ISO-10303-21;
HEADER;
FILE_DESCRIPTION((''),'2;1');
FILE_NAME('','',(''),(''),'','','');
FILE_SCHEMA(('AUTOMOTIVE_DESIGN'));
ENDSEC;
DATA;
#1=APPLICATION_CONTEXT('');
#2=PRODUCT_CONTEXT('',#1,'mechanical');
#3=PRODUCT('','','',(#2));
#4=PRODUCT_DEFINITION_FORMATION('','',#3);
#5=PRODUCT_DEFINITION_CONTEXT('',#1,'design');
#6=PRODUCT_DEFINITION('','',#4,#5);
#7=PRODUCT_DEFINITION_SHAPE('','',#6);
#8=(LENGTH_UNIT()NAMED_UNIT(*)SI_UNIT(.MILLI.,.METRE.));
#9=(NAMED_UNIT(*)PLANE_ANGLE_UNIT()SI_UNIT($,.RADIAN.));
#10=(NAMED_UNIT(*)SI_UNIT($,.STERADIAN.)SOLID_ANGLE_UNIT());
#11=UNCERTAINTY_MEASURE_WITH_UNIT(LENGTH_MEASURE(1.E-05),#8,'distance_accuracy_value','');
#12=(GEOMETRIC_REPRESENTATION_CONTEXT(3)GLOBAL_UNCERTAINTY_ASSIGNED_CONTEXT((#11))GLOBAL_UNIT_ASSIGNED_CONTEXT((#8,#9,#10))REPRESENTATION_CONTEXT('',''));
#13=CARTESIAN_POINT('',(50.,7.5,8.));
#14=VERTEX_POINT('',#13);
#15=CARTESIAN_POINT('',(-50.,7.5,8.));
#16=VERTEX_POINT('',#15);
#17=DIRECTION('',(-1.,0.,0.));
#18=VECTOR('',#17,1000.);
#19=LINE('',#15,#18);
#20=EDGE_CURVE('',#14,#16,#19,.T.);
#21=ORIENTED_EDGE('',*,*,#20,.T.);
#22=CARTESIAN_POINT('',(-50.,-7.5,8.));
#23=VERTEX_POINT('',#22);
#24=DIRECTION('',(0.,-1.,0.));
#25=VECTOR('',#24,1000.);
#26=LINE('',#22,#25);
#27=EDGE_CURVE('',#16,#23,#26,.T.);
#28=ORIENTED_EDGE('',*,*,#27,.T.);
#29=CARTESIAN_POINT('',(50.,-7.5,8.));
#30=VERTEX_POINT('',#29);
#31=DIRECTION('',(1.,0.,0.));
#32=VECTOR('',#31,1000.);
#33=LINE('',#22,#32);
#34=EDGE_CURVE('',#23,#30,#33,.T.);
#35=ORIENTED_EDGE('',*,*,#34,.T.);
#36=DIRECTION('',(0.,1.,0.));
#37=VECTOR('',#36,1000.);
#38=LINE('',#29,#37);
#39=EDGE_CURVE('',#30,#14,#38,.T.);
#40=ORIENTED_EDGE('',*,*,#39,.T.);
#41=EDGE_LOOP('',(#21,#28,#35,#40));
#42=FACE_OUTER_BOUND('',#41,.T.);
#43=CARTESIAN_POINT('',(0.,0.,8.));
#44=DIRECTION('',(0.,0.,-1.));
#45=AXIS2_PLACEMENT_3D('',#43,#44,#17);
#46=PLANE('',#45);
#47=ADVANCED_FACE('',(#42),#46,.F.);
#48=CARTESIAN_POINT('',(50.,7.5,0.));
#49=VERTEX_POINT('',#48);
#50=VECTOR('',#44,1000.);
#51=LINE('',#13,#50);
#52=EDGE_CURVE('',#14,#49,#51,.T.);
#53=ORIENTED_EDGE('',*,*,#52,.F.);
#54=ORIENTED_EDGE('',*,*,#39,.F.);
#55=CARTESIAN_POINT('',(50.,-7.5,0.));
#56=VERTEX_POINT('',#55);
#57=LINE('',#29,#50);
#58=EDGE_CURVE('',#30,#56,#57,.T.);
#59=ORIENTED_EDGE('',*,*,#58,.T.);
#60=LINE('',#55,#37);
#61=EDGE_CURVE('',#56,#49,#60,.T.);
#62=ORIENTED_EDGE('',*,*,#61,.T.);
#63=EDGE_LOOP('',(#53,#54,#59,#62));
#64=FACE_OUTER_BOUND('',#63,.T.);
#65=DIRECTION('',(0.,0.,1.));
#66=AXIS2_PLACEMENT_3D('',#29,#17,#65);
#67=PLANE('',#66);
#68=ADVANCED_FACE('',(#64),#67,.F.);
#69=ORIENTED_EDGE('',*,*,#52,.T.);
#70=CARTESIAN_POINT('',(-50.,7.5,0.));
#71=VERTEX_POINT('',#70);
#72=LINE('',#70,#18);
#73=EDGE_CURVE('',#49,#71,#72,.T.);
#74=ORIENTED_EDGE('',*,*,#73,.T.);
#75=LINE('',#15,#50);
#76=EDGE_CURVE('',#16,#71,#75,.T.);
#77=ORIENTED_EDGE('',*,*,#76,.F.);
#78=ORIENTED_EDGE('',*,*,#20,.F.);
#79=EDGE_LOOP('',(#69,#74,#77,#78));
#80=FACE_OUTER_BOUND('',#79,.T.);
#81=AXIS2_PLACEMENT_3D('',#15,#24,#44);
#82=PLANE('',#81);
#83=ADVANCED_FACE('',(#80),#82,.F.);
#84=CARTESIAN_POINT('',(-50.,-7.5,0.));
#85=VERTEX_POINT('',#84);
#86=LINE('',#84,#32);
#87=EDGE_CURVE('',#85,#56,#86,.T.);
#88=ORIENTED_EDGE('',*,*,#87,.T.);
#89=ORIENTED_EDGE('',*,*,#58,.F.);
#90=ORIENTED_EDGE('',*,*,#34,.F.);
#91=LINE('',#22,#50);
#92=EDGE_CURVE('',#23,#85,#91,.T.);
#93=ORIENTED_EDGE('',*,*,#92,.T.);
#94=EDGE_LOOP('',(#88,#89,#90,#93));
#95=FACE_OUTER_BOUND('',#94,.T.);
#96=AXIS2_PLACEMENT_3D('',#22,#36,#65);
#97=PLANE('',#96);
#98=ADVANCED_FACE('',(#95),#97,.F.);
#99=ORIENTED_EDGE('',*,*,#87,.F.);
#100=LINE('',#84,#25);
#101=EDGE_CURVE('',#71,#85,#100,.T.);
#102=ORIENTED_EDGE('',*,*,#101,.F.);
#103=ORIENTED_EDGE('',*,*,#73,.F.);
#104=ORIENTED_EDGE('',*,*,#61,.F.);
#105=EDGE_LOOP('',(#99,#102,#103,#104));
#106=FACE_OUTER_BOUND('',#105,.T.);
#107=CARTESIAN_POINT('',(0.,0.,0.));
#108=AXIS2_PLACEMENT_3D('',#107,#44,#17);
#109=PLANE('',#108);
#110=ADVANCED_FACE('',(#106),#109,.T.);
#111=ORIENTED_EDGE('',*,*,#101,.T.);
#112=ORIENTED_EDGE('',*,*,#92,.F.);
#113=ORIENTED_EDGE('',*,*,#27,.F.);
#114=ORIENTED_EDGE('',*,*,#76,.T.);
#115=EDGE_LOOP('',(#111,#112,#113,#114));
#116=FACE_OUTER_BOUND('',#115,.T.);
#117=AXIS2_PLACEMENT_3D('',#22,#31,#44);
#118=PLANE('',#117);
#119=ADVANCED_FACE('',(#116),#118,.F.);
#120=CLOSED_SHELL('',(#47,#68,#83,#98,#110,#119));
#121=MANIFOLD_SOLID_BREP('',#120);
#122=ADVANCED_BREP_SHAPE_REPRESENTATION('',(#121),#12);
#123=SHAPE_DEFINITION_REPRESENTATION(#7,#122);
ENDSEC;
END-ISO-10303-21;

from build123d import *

# Parameters (mm, degrees)
SKETCH_1_W      = 100
SKETCH_1_H      = 15
EXTRUDE_1_DEPTH = 8


with BuildPart() as part:
    # 草图1 → 凸台-拉伸1 (new body)
    with BuildSketch(Plane.XY):
        Rectangle(SKETCH_1_W, SKETCH_1_H)
    extrude(amount=EXTRUDE_1_DEPTH)


solid = part.part
